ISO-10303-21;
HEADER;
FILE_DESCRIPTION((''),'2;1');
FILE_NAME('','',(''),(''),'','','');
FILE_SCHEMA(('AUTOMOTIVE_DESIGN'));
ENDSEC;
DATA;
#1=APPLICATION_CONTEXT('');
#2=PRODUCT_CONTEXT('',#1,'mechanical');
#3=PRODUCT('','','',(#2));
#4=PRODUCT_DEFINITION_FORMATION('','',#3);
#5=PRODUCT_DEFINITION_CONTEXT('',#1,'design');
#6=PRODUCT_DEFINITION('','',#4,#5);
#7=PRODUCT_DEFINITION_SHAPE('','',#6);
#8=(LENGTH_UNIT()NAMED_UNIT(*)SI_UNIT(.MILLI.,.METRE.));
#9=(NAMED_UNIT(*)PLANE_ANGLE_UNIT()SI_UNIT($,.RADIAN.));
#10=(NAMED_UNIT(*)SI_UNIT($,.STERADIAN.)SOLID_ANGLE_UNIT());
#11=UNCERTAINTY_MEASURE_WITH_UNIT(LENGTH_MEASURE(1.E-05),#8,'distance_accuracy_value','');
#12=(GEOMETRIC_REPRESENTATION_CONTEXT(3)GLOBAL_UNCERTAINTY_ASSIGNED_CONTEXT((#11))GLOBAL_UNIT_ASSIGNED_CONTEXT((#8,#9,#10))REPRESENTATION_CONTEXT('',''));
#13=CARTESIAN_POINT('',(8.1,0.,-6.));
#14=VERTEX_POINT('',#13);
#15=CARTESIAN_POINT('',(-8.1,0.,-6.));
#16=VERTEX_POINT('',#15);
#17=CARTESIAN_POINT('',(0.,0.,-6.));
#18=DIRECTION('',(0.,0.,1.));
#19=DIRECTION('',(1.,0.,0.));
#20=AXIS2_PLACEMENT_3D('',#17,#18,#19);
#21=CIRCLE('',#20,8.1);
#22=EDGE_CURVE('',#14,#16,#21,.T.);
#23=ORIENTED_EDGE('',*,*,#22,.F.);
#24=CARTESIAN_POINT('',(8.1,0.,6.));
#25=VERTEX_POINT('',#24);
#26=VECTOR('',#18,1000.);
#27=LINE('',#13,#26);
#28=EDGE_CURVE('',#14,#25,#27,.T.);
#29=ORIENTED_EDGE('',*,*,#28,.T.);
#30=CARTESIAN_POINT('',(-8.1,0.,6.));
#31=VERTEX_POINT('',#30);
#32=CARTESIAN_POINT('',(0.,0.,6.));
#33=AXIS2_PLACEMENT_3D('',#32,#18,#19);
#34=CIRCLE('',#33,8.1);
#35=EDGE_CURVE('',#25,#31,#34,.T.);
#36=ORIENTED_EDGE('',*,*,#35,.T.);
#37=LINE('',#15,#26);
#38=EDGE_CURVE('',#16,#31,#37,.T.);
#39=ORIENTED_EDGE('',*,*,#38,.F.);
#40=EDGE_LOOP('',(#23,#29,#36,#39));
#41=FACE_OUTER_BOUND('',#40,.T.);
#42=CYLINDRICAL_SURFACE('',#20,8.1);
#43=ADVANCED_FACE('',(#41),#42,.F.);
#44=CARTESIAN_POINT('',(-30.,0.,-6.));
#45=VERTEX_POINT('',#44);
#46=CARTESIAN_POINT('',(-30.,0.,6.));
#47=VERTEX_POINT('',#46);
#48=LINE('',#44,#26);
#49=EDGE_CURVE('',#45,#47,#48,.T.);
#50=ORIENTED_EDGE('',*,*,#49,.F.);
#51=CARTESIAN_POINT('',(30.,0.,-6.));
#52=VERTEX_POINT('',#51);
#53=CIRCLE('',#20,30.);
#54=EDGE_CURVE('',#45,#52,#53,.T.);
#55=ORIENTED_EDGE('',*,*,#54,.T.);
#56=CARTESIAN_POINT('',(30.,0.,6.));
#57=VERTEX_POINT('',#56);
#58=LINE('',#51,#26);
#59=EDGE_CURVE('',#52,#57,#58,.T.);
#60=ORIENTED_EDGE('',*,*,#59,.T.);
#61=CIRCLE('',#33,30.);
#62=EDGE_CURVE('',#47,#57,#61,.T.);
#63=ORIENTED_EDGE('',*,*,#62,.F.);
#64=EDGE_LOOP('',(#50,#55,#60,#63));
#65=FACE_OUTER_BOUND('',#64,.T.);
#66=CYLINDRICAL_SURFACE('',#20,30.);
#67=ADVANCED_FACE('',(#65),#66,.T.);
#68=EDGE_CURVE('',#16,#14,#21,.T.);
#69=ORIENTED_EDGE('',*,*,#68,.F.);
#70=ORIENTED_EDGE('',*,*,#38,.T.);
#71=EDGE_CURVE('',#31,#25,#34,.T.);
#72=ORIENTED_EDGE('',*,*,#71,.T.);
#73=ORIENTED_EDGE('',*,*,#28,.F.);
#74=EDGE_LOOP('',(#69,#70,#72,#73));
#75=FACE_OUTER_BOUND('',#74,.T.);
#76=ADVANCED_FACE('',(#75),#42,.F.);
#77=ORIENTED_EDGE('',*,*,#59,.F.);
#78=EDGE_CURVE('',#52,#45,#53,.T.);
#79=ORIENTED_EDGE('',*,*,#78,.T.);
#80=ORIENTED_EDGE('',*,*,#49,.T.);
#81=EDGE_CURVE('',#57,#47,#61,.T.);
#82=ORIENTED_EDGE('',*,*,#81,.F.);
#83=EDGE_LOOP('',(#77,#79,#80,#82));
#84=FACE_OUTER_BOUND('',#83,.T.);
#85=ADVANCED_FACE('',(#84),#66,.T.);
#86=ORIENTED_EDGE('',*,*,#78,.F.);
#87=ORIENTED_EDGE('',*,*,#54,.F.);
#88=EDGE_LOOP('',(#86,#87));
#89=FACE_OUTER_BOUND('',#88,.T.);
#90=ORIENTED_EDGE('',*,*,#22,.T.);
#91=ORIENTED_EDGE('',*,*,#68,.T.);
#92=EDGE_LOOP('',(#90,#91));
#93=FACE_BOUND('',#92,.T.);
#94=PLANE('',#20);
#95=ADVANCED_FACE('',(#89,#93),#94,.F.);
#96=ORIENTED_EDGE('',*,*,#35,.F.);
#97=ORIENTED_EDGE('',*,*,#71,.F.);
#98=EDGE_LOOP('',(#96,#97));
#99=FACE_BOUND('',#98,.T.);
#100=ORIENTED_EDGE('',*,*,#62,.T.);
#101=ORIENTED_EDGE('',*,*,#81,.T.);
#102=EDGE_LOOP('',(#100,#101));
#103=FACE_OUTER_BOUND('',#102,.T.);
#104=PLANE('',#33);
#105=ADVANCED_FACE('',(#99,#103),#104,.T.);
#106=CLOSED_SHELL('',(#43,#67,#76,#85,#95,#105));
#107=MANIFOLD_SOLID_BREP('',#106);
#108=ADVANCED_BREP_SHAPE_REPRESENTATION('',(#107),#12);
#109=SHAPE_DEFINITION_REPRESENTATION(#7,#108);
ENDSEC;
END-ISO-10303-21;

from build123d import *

# Parameters (mm, degrees)
SKETCH_1_R      = 30
SKETCH_1_R_2    = 8.1
EXTRUDE_1_DEPTH = 6


with BuildPart() as part:
    # 草图1 → 凸台-拉伸1 (new, symmetric)
    with BuildSketch(Plane.XY):
        Circle(SKETCH_1_R)
        Circle(SKETCH_1_R_2, mode=Mode.SUBTRACT)
    extrude(amount=EXTRUDE_1_DEPTH, both=True)


solid = part.part
